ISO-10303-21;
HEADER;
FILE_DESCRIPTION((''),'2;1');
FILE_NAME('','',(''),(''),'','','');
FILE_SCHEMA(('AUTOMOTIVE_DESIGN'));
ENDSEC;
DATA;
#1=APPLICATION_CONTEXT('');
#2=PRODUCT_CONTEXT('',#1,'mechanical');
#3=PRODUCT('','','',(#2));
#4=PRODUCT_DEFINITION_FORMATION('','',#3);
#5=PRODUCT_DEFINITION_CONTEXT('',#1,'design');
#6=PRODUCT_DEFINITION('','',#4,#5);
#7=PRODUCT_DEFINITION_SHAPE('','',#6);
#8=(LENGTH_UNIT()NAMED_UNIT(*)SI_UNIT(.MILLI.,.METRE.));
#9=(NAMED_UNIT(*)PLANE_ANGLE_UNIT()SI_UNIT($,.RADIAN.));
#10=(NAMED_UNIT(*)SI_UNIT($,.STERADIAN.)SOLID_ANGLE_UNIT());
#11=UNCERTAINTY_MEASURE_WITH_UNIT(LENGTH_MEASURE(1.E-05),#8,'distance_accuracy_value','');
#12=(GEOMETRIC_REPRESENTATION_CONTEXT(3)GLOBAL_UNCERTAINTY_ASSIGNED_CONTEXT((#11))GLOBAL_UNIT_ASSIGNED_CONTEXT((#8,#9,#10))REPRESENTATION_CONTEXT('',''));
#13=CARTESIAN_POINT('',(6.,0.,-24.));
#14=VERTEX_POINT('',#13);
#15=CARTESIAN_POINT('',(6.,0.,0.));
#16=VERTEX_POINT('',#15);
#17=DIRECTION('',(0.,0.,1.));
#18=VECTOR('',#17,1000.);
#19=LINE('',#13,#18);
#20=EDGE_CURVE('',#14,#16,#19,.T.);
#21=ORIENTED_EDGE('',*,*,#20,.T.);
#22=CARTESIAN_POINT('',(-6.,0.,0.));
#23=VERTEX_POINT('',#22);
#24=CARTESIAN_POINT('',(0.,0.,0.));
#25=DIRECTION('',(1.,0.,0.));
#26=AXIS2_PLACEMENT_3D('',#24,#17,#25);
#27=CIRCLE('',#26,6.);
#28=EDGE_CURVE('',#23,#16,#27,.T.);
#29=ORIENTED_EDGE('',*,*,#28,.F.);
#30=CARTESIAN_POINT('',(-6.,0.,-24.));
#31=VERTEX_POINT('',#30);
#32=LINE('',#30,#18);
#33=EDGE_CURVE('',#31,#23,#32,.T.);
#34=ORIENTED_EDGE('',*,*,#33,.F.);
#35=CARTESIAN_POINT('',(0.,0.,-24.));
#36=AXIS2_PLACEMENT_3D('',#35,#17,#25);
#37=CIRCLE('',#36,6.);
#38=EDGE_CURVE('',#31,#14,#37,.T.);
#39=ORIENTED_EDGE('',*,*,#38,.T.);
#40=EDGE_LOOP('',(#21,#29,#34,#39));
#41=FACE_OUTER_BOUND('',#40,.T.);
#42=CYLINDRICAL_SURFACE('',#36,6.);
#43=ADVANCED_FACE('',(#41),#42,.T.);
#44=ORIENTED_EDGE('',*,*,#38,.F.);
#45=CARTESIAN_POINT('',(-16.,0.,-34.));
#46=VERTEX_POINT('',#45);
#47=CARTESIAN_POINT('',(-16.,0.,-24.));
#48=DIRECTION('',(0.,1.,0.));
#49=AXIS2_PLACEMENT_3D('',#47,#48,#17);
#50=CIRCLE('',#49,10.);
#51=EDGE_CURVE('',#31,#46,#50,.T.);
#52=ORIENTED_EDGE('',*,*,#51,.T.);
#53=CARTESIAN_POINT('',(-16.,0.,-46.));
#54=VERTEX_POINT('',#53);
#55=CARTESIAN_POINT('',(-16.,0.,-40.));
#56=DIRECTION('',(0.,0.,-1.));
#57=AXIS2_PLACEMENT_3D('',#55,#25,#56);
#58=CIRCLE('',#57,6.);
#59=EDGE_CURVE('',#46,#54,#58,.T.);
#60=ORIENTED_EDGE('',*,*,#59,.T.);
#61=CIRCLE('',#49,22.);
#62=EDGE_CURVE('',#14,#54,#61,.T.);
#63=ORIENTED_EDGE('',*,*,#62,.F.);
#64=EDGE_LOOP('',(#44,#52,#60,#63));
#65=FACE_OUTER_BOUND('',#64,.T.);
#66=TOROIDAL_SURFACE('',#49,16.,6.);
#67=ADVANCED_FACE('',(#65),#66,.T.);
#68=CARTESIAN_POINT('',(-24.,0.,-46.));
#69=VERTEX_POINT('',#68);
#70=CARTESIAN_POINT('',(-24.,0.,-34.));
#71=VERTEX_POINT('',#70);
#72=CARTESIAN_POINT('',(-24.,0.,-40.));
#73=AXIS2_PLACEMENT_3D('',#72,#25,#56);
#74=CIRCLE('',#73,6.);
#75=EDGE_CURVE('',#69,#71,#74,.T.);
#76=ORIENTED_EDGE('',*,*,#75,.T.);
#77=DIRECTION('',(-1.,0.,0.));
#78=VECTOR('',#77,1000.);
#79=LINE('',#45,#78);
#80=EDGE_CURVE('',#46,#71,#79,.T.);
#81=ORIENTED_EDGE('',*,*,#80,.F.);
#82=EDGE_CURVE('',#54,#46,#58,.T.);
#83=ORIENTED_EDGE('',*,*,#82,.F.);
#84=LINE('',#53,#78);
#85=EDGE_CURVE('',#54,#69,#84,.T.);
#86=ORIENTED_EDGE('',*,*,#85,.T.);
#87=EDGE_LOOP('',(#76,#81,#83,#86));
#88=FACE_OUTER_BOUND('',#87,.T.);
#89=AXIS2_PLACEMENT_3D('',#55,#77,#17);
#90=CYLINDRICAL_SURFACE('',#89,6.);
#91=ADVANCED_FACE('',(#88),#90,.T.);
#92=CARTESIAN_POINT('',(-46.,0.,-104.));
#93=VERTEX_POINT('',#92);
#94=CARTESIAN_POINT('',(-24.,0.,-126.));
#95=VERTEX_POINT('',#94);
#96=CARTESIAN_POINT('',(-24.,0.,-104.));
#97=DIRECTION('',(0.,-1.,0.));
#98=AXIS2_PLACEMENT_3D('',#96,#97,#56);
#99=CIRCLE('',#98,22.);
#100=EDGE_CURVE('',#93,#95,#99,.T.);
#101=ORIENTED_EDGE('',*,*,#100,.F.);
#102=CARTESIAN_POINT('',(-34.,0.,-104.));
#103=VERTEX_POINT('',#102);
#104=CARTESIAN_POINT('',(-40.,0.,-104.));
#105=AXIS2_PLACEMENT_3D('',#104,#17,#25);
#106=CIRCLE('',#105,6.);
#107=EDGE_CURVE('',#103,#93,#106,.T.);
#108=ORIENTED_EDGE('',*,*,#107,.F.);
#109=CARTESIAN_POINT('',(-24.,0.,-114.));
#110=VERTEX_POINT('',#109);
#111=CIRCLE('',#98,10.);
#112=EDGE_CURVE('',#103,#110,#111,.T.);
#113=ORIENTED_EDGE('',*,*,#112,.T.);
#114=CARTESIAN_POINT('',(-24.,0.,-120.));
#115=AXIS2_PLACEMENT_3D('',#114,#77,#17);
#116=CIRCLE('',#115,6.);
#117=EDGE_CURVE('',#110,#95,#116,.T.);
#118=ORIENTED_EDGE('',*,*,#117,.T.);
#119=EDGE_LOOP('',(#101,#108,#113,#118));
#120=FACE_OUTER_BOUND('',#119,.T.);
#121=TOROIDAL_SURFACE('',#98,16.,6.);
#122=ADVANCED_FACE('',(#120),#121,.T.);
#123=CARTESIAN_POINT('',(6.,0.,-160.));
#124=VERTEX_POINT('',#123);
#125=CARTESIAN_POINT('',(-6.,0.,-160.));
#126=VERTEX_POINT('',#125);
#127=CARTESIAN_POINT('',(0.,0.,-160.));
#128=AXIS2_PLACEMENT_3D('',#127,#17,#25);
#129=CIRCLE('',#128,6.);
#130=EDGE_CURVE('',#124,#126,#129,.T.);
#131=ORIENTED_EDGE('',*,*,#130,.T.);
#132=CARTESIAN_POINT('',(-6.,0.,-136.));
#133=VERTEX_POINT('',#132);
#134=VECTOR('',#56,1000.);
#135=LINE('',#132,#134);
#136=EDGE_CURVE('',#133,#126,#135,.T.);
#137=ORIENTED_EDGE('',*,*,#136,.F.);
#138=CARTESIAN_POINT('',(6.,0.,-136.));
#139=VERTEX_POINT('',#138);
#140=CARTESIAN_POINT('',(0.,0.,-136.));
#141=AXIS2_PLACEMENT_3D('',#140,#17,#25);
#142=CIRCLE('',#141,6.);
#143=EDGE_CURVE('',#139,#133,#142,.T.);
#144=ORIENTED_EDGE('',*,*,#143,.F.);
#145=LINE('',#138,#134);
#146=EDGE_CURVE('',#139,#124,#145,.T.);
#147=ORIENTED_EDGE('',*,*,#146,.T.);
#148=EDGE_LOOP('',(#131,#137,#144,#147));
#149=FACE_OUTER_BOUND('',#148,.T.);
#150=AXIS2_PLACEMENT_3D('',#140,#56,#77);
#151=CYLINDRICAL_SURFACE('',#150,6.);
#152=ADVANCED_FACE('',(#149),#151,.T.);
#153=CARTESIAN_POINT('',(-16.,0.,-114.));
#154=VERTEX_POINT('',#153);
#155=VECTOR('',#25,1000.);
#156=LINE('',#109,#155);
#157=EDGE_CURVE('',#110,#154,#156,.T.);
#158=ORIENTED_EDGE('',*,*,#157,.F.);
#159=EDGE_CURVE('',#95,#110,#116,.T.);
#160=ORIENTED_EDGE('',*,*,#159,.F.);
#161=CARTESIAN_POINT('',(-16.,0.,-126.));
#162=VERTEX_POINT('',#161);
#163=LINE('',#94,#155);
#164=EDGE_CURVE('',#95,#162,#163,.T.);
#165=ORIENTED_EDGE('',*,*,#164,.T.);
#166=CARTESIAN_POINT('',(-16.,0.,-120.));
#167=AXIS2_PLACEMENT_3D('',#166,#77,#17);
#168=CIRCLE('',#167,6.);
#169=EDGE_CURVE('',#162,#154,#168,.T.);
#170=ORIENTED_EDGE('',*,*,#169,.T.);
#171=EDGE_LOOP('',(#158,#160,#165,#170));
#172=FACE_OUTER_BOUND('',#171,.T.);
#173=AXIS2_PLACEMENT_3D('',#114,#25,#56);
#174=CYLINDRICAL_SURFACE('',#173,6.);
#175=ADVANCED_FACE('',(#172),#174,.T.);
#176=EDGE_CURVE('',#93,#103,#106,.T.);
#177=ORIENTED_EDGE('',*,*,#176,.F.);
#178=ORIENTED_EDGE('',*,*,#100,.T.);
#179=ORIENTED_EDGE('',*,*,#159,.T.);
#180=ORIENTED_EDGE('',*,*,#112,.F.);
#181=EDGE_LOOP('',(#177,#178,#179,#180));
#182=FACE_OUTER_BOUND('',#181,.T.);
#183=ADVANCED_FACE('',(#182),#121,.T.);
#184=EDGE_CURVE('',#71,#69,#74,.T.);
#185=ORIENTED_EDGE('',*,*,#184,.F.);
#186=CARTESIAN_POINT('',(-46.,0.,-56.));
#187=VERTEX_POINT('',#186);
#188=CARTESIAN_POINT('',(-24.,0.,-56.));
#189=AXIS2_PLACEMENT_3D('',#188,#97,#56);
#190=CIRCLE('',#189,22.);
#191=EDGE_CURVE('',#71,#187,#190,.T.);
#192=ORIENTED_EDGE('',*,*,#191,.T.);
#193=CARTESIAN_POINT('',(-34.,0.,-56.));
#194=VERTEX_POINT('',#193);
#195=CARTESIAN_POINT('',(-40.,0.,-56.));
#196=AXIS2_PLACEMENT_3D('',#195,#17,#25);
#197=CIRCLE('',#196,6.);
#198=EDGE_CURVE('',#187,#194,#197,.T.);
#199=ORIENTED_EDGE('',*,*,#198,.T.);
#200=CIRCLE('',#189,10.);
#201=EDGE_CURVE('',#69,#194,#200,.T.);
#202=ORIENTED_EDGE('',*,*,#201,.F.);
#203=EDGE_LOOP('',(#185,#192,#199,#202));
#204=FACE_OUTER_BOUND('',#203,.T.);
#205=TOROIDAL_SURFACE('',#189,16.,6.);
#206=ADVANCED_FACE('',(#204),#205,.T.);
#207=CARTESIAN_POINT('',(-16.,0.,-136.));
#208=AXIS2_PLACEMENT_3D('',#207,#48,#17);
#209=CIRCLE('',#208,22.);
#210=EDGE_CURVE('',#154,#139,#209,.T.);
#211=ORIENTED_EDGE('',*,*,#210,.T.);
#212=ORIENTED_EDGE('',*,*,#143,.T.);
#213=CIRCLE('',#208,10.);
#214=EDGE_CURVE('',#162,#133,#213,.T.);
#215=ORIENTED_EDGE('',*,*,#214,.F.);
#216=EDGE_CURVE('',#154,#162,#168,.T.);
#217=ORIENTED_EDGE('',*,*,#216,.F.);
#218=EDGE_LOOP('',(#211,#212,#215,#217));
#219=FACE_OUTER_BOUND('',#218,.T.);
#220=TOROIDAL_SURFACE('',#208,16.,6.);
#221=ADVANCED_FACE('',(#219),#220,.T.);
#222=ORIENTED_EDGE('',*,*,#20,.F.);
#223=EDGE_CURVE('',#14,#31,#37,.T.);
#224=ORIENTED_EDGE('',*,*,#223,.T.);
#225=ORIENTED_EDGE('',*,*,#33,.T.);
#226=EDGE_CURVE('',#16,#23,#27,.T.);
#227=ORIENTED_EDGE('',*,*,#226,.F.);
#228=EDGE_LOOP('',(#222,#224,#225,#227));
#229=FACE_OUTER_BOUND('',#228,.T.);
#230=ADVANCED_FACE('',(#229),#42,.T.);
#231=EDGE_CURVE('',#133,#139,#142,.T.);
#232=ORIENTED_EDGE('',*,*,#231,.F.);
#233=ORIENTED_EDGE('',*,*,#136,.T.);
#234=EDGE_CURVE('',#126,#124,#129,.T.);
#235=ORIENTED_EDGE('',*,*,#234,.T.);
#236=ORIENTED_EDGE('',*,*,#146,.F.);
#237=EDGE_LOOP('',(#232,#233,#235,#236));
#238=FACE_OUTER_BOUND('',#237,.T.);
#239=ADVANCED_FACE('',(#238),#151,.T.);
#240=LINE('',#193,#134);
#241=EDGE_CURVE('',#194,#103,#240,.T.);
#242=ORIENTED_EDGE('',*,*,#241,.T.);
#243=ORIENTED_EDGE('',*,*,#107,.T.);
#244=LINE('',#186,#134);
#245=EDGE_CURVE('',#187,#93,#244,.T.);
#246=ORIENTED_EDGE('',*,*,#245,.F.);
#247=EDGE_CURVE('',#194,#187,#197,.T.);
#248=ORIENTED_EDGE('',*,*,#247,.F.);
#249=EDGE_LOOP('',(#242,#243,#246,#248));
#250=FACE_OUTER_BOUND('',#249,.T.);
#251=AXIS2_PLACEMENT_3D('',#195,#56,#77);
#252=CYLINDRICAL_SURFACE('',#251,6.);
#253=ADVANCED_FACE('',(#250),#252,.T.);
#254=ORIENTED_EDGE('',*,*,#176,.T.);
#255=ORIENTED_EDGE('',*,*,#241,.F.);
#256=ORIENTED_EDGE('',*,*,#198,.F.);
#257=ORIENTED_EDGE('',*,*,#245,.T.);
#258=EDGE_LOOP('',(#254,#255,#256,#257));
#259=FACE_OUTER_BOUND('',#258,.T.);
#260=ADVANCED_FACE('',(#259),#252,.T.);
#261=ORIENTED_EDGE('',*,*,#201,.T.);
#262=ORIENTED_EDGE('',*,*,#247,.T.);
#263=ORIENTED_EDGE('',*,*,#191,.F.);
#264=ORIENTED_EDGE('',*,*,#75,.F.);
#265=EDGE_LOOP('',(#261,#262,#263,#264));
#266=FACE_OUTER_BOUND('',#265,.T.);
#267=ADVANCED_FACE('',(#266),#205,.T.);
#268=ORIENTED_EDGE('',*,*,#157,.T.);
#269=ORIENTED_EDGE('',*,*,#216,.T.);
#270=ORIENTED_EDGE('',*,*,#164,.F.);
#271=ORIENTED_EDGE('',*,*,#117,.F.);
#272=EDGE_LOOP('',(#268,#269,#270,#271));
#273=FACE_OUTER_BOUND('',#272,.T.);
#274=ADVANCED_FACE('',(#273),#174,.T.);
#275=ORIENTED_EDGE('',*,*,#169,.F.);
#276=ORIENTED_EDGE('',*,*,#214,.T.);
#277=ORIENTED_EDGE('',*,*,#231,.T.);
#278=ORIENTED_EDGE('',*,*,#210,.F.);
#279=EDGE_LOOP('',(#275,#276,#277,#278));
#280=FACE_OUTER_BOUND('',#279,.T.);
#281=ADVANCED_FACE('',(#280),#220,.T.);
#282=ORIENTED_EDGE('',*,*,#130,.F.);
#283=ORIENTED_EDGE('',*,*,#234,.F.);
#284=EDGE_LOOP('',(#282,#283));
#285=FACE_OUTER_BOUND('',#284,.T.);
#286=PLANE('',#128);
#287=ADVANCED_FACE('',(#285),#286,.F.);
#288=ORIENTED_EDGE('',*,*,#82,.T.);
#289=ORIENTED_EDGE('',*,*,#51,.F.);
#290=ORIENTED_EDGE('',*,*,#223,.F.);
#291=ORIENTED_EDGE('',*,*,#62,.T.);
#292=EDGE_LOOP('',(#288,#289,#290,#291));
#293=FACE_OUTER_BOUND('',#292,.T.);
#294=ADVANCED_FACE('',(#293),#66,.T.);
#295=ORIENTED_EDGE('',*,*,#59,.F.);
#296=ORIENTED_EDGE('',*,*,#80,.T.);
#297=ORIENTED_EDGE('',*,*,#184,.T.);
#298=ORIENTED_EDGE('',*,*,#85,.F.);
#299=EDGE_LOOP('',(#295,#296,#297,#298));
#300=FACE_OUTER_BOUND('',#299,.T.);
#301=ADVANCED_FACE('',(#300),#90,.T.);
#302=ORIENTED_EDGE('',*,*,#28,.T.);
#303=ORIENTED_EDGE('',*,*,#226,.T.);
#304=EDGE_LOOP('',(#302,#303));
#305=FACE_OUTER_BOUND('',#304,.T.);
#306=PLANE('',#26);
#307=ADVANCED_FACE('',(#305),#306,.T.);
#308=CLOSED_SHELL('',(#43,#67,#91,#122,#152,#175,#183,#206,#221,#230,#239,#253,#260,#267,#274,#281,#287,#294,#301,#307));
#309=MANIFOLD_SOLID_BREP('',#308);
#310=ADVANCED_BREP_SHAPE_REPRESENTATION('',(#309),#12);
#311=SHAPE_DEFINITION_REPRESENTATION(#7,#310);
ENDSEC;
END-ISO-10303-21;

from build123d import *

# Parameters (mm, degrees)
SKETCH2_R = 6


with BuildPart() as part:
    # Sweep1: sweep along a path in Sketch1
    with BuildLine(Plane(origin=(0, 0, 0), x_dir=(1, 0, 0), z_dir=(0, 1, 0))) as sweep1_path:
        Line((0, 160), (0, 136))
        ThreePointArc((0, 136), (-4.686291501, 124.686291501), (-16, 120))
        Line((-16, 120), (-24, 120))
        ThreePointArc((-24, 120), (-35.313708499, 115.313708499), (-40, 104))
        Line((-40, 104), (-40, 56))
        ThreePointArc((-40, 56), (-35.313708499, 44.686291501), (-24, 40))
        Line((-24, 40), (-16, 40))
        ThreePointArc((-16, 40), (-4.686291501, 35.313708499), (0, 24))
        Line((0, 24), (0, 0))
    # Sketch2 → Sweep1 (sweep)
    with BuildSketch(Plane.XY):
        Circle(SKETCH2_R)
    sweep(path=sweep1_path.line)


solid = part.part
